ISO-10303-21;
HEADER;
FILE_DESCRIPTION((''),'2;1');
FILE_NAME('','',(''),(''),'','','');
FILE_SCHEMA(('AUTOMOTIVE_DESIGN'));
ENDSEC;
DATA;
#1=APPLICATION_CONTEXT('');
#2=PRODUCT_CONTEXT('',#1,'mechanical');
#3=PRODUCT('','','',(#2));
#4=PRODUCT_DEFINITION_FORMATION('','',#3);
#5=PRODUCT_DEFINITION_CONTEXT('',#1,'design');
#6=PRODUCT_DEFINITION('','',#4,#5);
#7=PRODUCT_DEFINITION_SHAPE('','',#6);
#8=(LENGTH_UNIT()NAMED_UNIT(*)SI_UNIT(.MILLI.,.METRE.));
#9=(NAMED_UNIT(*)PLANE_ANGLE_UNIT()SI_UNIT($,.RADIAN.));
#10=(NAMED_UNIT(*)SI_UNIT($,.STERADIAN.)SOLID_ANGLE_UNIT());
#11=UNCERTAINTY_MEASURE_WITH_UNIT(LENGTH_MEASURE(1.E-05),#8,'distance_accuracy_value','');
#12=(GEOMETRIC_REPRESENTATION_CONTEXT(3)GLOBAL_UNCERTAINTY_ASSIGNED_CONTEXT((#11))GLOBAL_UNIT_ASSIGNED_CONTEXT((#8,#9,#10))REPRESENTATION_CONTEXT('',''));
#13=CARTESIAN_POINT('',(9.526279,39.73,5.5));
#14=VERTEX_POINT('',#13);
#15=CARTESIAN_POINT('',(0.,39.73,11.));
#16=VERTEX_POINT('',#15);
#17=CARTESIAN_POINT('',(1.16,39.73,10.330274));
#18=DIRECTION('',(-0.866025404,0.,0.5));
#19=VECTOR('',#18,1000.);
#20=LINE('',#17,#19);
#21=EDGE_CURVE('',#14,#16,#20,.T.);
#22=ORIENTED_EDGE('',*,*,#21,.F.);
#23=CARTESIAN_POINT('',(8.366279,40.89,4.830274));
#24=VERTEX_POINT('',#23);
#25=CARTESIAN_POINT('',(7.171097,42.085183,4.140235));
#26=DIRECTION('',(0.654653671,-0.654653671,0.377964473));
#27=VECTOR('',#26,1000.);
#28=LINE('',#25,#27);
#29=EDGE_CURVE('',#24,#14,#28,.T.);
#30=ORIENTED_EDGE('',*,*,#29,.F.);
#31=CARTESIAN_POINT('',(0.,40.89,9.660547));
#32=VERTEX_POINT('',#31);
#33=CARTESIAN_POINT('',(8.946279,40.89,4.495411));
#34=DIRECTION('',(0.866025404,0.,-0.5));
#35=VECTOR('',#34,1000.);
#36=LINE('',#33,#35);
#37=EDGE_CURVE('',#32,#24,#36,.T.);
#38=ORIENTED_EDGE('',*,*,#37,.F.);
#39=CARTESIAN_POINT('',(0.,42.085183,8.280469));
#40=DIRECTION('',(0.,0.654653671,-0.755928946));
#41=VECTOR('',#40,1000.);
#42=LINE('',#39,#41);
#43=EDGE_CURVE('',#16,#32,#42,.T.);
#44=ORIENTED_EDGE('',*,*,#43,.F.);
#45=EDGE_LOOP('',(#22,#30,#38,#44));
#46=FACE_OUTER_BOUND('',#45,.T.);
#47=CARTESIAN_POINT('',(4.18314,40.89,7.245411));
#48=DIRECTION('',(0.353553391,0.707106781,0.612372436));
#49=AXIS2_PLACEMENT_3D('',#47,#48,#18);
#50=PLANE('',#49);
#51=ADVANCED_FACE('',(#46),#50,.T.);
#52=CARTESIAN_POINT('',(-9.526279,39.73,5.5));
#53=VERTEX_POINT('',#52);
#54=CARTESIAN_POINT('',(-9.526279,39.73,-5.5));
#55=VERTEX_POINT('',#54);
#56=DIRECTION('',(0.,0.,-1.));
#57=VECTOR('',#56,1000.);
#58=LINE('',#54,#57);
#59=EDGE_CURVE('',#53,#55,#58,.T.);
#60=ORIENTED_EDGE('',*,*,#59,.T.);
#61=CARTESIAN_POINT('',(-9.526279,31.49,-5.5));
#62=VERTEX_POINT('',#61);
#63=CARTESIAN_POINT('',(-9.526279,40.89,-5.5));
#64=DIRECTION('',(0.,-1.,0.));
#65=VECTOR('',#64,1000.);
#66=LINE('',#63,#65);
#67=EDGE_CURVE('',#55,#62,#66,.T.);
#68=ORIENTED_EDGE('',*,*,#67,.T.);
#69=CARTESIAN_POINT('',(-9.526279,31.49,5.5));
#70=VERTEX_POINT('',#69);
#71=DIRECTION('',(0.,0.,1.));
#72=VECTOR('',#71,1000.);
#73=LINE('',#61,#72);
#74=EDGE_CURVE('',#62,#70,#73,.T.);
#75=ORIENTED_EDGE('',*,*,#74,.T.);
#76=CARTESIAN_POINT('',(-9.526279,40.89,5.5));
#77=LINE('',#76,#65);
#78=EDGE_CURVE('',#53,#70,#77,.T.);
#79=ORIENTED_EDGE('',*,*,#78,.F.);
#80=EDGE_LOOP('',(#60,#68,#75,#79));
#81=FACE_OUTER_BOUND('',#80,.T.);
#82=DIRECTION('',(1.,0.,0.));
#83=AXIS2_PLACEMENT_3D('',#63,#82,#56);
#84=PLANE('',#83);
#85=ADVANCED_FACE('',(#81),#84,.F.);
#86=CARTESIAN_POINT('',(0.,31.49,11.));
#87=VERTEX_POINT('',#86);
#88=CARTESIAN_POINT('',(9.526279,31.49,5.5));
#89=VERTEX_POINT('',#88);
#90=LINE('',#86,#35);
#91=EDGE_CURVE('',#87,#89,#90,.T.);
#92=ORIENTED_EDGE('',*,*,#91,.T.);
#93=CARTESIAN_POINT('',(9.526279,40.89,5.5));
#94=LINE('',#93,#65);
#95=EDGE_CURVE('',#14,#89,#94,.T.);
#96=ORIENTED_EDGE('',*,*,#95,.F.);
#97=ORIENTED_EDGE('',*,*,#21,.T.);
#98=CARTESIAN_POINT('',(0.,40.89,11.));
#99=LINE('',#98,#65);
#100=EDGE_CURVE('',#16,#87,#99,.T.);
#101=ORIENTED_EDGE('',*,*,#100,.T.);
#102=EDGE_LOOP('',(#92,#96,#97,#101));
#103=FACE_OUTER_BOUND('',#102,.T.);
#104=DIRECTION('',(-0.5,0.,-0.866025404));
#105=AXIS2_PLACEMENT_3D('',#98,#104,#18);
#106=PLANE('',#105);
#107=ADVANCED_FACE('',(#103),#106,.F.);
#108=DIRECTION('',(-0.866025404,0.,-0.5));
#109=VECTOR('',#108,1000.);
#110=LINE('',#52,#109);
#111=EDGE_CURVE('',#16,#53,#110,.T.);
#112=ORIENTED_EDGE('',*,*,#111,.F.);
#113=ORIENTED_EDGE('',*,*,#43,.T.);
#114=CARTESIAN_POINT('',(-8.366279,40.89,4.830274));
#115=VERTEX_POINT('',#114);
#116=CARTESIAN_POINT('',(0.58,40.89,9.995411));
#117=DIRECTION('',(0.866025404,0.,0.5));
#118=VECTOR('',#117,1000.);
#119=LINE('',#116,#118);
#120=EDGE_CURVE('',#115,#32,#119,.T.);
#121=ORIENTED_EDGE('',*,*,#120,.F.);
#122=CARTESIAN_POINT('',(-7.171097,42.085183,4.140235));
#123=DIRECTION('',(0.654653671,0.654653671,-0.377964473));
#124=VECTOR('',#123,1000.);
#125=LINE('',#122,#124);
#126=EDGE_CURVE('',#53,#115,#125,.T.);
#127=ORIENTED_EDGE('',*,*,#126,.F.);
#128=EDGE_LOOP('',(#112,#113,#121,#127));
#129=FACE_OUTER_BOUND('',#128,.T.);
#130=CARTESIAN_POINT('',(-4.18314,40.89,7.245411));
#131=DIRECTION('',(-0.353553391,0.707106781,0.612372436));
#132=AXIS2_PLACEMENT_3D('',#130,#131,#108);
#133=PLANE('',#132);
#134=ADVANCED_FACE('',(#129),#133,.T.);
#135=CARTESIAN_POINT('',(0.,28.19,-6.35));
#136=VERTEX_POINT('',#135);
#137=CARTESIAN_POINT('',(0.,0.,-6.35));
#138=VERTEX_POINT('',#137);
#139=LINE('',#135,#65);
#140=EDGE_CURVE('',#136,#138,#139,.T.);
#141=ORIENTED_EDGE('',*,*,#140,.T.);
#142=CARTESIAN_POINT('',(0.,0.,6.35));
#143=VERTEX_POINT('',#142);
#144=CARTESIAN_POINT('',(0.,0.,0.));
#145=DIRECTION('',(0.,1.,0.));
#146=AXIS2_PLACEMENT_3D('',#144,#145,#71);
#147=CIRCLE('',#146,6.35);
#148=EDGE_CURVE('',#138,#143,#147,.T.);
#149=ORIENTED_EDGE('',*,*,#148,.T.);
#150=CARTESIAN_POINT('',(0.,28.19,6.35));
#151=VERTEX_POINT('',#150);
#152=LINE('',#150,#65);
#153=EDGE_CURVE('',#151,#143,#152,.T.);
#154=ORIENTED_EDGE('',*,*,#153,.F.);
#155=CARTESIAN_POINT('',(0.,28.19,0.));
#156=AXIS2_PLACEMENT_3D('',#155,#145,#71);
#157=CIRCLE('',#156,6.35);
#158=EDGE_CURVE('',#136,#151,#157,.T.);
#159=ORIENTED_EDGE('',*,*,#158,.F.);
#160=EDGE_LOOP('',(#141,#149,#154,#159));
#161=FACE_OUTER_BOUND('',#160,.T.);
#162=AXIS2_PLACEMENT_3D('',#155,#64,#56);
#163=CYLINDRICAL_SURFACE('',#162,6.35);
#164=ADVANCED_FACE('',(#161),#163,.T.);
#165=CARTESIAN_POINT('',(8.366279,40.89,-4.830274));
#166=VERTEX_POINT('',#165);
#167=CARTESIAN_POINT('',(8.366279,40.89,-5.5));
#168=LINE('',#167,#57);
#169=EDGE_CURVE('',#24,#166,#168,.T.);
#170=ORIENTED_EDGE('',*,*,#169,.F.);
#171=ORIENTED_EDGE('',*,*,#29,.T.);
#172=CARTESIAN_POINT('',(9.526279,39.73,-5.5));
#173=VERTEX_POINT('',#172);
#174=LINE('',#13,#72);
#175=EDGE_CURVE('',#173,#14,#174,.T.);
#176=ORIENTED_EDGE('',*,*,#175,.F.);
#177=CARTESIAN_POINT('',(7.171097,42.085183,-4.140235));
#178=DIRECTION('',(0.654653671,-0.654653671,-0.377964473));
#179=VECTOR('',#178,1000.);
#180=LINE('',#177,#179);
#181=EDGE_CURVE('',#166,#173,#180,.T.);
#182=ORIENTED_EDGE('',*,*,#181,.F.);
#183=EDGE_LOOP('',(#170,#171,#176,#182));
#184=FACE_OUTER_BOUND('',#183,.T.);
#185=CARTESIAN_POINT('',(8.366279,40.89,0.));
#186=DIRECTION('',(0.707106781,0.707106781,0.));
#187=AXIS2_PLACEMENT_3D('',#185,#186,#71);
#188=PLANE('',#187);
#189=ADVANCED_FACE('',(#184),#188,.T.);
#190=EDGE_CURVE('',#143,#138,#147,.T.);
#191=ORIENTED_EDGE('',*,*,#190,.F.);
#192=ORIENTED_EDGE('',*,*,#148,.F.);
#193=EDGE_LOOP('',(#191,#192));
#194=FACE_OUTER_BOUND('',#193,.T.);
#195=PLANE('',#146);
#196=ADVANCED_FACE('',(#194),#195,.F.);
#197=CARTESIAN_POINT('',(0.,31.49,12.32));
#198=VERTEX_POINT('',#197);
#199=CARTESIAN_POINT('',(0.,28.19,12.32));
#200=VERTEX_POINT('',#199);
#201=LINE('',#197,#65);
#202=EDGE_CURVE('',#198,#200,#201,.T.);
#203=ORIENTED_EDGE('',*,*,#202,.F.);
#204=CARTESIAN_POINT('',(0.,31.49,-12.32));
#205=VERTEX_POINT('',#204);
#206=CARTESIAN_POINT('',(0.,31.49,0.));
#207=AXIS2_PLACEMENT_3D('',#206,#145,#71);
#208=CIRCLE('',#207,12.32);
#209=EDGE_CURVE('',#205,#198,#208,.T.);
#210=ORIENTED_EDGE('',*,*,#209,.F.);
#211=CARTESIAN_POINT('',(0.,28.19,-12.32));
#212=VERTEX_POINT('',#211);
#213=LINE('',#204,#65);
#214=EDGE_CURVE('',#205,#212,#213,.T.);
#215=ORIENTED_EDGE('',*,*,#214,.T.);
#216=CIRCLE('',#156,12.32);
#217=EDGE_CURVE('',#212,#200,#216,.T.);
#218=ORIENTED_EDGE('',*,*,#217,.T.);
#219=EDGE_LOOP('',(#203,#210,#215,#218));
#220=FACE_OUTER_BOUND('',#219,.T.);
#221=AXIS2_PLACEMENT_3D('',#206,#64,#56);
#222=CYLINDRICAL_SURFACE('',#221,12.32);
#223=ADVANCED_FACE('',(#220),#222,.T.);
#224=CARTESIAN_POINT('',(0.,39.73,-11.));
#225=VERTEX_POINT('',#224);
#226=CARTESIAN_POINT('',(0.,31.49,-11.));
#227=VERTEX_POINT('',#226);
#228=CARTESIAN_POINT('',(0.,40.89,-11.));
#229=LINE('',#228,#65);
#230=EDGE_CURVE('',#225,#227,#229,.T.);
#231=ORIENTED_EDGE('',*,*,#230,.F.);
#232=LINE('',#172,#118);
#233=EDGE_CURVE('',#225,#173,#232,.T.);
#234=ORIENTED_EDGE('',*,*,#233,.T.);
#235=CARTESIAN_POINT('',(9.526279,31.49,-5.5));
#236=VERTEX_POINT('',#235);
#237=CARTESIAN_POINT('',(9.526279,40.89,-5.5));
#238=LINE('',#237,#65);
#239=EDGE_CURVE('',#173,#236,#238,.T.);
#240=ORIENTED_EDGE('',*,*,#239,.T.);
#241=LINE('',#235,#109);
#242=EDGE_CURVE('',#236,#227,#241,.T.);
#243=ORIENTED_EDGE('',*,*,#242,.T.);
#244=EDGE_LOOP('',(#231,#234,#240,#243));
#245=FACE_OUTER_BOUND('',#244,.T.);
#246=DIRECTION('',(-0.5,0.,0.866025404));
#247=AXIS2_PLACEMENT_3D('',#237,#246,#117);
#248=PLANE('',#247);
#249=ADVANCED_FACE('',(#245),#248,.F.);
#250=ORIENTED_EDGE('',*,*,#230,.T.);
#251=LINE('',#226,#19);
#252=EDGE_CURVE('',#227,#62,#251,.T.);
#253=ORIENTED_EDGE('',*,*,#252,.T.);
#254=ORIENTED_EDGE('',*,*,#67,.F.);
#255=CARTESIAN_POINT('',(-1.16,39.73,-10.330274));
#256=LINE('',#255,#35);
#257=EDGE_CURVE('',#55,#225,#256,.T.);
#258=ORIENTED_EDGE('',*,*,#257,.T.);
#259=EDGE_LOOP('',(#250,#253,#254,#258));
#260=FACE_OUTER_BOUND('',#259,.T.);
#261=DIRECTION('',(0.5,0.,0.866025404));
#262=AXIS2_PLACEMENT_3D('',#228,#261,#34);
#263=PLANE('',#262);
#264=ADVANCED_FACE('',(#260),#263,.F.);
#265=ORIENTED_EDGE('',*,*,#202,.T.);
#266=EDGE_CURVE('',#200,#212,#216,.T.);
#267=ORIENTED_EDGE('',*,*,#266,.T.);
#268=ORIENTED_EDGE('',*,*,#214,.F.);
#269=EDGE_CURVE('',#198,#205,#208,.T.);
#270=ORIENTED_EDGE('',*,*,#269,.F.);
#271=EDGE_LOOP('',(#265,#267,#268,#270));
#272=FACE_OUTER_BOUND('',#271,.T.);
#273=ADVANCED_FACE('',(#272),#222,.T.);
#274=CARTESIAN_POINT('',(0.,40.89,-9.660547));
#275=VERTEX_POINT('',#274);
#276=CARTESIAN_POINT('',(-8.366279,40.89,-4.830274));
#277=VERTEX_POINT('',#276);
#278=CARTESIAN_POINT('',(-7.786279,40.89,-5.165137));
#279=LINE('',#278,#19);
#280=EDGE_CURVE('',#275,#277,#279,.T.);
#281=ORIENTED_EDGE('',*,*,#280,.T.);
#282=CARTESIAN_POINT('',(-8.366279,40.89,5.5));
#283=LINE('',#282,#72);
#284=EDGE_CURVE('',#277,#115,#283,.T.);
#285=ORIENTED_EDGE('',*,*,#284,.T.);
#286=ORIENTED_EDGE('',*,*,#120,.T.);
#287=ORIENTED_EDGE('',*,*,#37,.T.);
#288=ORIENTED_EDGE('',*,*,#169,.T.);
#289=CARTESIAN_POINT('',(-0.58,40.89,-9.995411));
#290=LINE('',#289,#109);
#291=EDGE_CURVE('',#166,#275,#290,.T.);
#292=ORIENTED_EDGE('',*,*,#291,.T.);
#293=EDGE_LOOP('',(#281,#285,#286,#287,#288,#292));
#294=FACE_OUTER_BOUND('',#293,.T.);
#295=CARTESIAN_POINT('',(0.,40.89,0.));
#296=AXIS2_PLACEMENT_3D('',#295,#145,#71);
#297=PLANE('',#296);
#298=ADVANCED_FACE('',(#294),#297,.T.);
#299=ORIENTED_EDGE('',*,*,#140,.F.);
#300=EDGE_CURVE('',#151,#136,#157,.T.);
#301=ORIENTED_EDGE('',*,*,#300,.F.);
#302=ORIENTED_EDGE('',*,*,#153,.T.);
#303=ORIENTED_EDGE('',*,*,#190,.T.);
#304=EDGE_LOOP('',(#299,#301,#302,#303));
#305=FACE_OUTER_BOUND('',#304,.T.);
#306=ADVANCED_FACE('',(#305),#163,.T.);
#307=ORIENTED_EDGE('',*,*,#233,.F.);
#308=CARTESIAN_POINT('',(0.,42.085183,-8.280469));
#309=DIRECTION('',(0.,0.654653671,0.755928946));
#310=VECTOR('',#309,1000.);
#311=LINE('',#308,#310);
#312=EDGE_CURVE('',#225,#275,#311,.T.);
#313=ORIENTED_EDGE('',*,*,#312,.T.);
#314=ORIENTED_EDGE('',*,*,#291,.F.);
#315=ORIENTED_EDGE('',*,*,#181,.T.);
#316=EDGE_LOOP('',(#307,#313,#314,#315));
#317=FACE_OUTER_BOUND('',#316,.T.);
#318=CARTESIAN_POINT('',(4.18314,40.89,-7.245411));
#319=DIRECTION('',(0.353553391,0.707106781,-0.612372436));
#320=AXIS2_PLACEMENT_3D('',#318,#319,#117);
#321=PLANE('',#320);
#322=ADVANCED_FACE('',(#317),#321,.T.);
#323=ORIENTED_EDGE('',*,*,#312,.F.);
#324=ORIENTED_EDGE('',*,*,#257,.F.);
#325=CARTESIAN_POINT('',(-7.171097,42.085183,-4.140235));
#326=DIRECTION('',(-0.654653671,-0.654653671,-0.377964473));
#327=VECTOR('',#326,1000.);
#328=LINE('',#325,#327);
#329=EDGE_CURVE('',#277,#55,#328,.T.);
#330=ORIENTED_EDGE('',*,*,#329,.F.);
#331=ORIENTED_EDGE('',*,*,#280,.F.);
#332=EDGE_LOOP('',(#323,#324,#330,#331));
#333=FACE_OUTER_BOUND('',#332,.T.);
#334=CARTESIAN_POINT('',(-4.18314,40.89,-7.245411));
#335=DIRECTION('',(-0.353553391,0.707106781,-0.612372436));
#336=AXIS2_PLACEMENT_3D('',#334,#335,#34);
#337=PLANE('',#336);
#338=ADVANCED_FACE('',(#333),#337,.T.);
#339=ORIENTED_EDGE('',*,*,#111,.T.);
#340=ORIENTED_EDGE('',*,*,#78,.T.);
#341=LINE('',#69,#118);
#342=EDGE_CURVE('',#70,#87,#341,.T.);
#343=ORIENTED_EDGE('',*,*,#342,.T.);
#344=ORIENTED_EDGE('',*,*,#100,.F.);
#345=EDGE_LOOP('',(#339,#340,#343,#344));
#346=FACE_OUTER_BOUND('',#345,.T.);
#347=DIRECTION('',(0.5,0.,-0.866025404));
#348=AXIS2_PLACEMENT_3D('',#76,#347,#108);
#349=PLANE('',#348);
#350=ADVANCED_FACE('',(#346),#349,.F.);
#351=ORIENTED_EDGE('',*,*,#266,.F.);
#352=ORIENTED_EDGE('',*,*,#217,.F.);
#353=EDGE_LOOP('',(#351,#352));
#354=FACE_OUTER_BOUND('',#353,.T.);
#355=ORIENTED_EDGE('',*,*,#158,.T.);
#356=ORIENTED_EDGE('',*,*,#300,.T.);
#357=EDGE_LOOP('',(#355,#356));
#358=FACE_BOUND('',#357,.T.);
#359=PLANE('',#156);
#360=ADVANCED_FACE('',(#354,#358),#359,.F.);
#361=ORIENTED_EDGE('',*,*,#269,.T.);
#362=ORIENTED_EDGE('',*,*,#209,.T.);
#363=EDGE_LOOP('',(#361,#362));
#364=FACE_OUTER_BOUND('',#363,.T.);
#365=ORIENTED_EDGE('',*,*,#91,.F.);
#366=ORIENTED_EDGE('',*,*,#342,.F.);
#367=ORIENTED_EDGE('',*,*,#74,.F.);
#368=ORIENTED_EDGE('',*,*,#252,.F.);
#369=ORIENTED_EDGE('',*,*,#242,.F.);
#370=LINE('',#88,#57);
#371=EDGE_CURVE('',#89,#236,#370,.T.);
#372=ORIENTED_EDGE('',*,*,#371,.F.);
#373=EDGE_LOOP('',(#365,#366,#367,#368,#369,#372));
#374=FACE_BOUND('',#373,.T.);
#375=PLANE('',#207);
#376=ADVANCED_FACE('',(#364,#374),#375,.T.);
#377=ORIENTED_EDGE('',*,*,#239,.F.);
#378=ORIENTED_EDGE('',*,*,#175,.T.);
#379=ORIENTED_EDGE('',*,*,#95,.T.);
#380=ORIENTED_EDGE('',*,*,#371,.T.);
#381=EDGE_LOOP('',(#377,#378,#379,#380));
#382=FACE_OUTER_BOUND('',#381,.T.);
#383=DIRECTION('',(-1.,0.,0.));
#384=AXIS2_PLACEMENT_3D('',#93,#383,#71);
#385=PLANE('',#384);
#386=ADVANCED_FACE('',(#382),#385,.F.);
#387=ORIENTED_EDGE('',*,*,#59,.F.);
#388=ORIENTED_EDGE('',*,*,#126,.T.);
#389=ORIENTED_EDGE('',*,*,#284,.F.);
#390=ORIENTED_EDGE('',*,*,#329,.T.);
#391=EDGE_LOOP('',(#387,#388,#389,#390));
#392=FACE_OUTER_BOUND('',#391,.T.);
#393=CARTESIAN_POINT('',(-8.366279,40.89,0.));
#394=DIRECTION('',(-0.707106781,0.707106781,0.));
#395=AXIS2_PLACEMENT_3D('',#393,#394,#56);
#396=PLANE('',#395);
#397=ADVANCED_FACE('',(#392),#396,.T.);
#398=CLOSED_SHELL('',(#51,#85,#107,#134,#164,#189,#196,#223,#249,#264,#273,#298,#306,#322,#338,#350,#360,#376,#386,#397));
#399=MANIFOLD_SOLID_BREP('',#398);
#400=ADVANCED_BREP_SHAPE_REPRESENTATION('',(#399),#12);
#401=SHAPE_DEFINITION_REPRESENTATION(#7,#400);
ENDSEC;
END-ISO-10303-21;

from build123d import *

# Parameters (mm, degrees)
SHANK_SKETCH_12_7_R         = 6.35
SHANK_12_7_DEPTH            = 28.19
FLANGE_SKETCH_24_64_R       = 12.32
FLANGE_24_64_DEPTH          = 3.3
HEX_HEAD_DEPTH              = 9.4
EDGE_CHAMFER_1_16X45_A_SIZE = 1.16
EDGE_CHAMFER_1_16X45_B_SIZE = 1.16
EDGE_CHAMFER_1_16X45_C_SIZE = 1.16


with BuildPart() as part:
    # Shank Sketch Ø12.7 → Shank Ø12.7 (new body)
    with BuildSketch(Plane(origin=(0, 0, 0), x_dir=(1, 0, 0), z_dir=(0, 1, 0))):
        with Locations(Location((0, 0, 0), (0, 0, 90))):
            Circle(SHANK_SKETCH_12_7_R)
    extrude(amount=SHANK_12_7_DEPTH)

    # Flange Sketch Ø24.64 → Flange Ø24.64 (add)
    with BuildSketch(Plane(origin=(0, 28.19, 0), x_dir=(1, 0, 0), z_dir=(0, 1, 0))):
        with Locations(Location((0, 0, 0), (0, 0, 270))):
            Circle(FLANGE_SKETCH_24_64_R)
    extrude(amount=FLANGE_24_64_DEPTH)

    # Hex Head Sketch → Hex Head (add)
    with BuildSketch(Plane(origin=(0, 31.49, 0), x_dir=(1, 0, 0), z_dir=(0, 1, 0))):
        Polygon((0, 11), (-9.526279442, 5.5), (-9.526279442, -5.5), (0, -11), (9.526279442, -5.5), (9.526279442, 5.5), align=None)
    extrude(amount=HEX_HEAD_DEPTH)

    # Edge Chamfer 1.16x45 A
    edge_chamfer_1_16x45_a_edges = [part.edges().sort_by_distance(p)[0] for p in [
        (-9.526279442, 40.89, 0),
        (-4.763139721, 40.89, 8.25),
    ]]
    chamfer(edge_chamfer_1_16x45_a_edges, length=EDGE_CHAMFER_1_16X45_A_SIZE)

    # Edge Chamfer 1.16x45 B
    edge_chamfer_1_16x45_b_edges = [part.edges().sort_by_distance(p)[0] for p in [
        (4.763139721, 40.89, -8.25),
        (9.526279442, 40.89, 0),
        (5.343139721, 40.89, 7.915136844),
    ]]
    chamfer(edge_chamfer_1_16x45_b_edges, length=EDGE_CHAMFER_1_16X45_B_SIZE)

    # Edge Chamfer 1.16x45 C
    edge_chamfer_1_16x45_c_edges = [part.edges().sort_by_distance(p)[0] for p in [
        (-4.763139721, 40.89, -8.25),
    ]]
    chamfer(edge_chamfer_1_16x45_c_edges, length=EDGE_CHAMFER_1_16X45_C_SIZE)


solid = part.part
